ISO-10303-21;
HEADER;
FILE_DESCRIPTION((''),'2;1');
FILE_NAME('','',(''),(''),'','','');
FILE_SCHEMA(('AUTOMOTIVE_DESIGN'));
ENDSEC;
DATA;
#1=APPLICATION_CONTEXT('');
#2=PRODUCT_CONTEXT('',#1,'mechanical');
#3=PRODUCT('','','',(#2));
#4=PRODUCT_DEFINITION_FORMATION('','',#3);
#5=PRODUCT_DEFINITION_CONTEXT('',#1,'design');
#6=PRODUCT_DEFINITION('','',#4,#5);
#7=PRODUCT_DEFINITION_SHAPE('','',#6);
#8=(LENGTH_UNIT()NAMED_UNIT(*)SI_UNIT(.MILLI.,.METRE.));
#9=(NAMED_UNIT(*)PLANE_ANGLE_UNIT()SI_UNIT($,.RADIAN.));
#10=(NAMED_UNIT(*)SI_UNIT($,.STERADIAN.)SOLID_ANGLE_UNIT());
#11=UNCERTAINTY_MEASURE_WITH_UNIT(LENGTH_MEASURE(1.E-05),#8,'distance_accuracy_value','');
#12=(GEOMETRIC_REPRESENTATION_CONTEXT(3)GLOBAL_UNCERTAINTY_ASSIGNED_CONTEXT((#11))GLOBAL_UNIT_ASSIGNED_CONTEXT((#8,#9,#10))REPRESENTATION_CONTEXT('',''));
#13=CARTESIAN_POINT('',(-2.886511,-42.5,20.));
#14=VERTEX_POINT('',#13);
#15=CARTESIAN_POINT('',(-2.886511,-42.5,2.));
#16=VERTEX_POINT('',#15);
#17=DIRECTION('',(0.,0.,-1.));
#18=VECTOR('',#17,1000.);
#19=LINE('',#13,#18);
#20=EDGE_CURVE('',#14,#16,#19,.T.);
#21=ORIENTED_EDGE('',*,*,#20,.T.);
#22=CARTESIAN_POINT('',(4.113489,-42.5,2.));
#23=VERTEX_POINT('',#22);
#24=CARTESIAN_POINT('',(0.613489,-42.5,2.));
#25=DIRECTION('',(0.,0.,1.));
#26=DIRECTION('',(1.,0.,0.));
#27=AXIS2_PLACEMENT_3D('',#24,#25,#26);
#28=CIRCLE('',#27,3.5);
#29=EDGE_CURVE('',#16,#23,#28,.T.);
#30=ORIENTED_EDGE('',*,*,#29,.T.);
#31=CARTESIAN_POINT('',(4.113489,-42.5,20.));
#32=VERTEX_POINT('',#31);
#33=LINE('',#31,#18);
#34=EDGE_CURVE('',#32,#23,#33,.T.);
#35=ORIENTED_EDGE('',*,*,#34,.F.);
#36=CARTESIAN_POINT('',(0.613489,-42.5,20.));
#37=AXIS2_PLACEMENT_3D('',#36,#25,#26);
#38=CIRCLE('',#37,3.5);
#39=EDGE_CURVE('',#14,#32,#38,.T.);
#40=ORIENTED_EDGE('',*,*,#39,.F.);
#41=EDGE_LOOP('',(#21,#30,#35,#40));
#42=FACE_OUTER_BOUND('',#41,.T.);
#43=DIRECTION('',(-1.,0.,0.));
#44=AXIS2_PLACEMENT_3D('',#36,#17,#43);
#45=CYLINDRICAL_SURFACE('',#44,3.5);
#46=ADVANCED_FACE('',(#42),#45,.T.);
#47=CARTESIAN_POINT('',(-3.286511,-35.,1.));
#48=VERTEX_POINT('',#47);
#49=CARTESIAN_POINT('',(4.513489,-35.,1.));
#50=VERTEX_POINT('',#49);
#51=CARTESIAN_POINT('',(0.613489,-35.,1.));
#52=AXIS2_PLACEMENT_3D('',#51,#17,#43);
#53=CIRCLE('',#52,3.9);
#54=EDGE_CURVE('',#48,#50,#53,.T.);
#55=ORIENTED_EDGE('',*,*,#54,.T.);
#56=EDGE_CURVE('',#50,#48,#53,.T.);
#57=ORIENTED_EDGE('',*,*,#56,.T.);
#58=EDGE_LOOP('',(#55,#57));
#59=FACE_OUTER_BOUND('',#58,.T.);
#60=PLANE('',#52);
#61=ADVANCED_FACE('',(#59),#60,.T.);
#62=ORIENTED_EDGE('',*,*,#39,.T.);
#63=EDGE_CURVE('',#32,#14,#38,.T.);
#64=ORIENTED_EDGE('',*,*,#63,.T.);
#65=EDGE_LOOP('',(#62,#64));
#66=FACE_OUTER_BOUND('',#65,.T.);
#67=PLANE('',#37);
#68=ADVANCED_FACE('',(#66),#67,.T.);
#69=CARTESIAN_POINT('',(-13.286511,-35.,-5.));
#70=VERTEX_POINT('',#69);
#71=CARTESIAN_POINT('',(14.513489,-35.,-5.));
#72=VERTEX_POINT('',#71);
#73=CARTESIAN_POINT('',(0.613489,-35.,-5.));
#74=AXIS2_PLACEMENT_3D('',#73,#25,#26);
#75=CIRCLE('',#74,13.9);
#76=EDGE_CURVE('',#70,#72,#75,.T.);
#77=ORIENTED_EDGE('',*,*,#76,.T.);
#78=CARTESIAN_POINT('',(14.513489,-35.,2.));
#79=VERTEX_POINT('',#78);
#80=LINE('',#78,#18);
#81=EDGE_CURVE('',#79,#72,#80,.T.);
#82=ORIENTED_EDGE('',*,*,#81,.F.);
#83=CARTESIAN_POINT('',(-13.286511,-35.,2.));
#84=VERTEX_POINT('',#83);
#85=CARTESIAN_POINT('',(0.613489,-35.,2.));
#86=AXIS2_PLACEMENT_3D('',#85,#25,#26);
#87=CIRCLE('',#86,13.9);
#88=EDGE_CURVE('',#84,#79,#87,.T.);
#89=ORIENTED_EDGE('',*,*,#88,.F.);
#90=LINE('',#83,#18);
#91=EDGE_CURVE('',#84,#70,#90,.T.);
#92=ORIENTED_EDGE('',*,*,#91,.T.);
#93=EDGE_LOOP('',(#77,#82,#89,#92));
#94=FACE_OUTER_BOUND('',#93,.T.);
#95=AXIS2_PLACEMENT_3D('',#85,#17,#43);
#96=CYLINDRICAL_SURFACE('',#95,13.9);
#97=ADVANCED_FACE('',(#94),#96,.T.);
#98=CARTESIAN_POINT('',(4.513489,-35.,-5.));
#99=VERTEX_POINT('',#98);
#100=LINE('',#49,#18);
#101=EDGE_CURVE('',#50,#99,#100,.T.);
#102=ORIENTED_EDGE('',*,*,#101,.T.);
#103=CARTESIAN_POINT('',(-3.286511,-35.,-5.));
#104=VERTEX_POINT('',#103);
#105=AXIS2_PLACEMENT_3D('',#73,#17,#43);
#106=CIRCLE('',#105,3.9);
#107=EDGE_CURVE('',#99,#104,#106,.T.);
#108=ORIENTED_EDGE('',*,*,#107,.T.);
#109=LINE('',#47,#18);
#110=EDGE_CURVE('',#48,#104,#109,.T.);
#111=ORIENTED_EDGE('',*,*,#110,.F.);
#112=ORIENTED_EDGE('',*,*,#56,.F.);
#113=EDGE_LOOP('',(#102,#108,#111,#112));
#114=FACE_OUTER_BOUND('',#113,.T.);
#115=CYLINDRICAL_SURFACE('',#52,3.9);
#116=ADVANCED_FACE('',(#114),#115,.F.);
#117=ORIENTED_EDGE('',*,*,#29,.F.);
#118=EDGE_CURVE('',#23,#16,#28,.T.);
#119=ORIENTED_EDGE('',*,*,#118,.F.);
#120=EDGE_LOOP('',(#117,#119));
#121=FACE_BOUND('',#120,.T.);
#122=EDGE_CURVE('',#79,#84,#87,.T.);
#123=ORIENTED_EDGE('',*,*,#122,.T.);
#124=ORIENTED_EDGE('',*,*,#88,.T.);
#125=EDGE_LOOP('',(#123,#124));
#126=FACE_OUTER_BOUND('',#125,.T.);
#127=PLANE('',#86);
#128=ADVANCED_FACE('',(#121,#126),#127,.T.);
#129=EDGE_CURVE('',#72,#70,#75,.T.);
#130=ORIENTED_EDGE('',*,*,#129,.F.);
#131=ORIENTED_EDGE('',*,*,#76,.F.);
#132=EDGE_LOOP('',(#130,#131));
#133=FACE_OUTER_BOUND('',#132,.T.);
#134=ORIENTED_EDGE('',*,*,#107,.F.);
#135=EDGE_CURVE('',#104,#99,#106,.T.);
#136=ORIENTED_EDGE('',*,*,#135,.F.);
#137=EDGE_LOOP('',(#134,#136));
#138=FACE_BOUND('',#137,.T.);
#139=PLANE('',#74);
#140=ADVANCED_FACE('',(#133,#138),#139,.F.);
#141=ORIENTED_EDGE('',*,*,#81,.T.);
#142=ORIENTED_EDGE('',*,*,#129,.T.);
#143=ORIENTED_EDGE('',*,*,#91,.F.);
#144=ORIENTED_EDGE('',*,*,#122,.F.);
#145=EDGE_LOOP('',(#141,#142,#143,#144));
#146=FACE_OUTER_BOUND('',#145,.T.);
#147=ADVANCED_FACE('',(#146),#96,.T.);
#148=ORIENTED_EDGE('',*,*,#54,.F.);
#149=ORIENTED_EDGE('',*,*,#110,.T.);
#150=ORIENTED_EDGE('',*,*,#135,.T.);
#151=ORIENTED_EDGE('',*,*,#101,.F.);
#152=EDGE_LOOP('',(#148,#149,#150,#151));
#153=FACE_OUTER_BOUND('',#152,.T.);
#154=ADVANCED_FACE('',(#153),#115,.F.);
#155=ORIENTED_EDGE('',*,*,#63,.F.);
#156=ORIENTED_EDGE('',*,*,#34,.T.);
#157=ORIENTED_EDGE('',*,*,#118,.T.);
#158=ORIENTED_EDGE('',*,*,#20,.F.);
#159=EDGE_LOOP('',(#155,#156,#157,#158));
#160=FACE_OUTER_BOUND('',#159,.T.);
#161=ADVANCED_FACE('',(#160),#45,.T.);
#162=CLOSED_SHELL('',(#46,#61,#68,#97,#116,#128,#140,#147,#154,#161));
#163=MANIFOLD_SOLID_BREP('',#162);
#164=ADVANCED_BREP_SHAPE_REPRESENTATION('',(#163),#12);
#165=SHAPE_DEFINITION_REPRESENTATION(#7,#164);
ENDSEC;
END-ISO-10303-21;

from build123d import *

# Parameters (mm, degrees)
BOSS_EXTRUDE1_DEPTH      = 2
BOSS_EXTRUDE1_DEPTH_BACK = 5
SKETCH1_R                = 13.9
SKETCH2_R                = 3.9
CUT_EXTRUDE1_DEPTH       = 6
SKETCH3_R                = 3.5
BOSS_EXTRUDE2_DEPTH      = 18


with BuildPart() as part:
    # Sketch1 → Boss-Extrude1 (new, two sides: drawn at the far end of the back side and taken through both)
    with BuildSketch(Plane.XY.offset(-BOSS_EXTRUDE1_DEPTH_BACK)):
        with Locations((0.613489308, -35)):
            Circle(SKETCH1_R)
    extrude(amount=BOSS_EXTRUDE1_DEPTH + BOSS_EXTRUDE1_DEPTH_BACK)

    # Sketch2 → Cut-Extrude1 (cut)
    with BuildSketch(Plane(origin=(0, 0, -5), x_dir=(-1, 0, 0), z_dir=(0, 0, -1))):
        with Locations((-0.613489308, -35)):
            Circle(SKETCH2_R)
    extrude(amount=-CUT_EXTRUDE1_DEPTH, mode=Mode.SUBTRACT)

    # Sketch3 → Boss-Extrude2 (add)
    with BuildSketch(Plane.XY.offset(2)):
        with Locations((0.613489308, -42.5)):
            Circle(SKETCH3_R)
    extrude(amount=BOSS_EXTRUDE2_DEPTH)


solid = part.part
